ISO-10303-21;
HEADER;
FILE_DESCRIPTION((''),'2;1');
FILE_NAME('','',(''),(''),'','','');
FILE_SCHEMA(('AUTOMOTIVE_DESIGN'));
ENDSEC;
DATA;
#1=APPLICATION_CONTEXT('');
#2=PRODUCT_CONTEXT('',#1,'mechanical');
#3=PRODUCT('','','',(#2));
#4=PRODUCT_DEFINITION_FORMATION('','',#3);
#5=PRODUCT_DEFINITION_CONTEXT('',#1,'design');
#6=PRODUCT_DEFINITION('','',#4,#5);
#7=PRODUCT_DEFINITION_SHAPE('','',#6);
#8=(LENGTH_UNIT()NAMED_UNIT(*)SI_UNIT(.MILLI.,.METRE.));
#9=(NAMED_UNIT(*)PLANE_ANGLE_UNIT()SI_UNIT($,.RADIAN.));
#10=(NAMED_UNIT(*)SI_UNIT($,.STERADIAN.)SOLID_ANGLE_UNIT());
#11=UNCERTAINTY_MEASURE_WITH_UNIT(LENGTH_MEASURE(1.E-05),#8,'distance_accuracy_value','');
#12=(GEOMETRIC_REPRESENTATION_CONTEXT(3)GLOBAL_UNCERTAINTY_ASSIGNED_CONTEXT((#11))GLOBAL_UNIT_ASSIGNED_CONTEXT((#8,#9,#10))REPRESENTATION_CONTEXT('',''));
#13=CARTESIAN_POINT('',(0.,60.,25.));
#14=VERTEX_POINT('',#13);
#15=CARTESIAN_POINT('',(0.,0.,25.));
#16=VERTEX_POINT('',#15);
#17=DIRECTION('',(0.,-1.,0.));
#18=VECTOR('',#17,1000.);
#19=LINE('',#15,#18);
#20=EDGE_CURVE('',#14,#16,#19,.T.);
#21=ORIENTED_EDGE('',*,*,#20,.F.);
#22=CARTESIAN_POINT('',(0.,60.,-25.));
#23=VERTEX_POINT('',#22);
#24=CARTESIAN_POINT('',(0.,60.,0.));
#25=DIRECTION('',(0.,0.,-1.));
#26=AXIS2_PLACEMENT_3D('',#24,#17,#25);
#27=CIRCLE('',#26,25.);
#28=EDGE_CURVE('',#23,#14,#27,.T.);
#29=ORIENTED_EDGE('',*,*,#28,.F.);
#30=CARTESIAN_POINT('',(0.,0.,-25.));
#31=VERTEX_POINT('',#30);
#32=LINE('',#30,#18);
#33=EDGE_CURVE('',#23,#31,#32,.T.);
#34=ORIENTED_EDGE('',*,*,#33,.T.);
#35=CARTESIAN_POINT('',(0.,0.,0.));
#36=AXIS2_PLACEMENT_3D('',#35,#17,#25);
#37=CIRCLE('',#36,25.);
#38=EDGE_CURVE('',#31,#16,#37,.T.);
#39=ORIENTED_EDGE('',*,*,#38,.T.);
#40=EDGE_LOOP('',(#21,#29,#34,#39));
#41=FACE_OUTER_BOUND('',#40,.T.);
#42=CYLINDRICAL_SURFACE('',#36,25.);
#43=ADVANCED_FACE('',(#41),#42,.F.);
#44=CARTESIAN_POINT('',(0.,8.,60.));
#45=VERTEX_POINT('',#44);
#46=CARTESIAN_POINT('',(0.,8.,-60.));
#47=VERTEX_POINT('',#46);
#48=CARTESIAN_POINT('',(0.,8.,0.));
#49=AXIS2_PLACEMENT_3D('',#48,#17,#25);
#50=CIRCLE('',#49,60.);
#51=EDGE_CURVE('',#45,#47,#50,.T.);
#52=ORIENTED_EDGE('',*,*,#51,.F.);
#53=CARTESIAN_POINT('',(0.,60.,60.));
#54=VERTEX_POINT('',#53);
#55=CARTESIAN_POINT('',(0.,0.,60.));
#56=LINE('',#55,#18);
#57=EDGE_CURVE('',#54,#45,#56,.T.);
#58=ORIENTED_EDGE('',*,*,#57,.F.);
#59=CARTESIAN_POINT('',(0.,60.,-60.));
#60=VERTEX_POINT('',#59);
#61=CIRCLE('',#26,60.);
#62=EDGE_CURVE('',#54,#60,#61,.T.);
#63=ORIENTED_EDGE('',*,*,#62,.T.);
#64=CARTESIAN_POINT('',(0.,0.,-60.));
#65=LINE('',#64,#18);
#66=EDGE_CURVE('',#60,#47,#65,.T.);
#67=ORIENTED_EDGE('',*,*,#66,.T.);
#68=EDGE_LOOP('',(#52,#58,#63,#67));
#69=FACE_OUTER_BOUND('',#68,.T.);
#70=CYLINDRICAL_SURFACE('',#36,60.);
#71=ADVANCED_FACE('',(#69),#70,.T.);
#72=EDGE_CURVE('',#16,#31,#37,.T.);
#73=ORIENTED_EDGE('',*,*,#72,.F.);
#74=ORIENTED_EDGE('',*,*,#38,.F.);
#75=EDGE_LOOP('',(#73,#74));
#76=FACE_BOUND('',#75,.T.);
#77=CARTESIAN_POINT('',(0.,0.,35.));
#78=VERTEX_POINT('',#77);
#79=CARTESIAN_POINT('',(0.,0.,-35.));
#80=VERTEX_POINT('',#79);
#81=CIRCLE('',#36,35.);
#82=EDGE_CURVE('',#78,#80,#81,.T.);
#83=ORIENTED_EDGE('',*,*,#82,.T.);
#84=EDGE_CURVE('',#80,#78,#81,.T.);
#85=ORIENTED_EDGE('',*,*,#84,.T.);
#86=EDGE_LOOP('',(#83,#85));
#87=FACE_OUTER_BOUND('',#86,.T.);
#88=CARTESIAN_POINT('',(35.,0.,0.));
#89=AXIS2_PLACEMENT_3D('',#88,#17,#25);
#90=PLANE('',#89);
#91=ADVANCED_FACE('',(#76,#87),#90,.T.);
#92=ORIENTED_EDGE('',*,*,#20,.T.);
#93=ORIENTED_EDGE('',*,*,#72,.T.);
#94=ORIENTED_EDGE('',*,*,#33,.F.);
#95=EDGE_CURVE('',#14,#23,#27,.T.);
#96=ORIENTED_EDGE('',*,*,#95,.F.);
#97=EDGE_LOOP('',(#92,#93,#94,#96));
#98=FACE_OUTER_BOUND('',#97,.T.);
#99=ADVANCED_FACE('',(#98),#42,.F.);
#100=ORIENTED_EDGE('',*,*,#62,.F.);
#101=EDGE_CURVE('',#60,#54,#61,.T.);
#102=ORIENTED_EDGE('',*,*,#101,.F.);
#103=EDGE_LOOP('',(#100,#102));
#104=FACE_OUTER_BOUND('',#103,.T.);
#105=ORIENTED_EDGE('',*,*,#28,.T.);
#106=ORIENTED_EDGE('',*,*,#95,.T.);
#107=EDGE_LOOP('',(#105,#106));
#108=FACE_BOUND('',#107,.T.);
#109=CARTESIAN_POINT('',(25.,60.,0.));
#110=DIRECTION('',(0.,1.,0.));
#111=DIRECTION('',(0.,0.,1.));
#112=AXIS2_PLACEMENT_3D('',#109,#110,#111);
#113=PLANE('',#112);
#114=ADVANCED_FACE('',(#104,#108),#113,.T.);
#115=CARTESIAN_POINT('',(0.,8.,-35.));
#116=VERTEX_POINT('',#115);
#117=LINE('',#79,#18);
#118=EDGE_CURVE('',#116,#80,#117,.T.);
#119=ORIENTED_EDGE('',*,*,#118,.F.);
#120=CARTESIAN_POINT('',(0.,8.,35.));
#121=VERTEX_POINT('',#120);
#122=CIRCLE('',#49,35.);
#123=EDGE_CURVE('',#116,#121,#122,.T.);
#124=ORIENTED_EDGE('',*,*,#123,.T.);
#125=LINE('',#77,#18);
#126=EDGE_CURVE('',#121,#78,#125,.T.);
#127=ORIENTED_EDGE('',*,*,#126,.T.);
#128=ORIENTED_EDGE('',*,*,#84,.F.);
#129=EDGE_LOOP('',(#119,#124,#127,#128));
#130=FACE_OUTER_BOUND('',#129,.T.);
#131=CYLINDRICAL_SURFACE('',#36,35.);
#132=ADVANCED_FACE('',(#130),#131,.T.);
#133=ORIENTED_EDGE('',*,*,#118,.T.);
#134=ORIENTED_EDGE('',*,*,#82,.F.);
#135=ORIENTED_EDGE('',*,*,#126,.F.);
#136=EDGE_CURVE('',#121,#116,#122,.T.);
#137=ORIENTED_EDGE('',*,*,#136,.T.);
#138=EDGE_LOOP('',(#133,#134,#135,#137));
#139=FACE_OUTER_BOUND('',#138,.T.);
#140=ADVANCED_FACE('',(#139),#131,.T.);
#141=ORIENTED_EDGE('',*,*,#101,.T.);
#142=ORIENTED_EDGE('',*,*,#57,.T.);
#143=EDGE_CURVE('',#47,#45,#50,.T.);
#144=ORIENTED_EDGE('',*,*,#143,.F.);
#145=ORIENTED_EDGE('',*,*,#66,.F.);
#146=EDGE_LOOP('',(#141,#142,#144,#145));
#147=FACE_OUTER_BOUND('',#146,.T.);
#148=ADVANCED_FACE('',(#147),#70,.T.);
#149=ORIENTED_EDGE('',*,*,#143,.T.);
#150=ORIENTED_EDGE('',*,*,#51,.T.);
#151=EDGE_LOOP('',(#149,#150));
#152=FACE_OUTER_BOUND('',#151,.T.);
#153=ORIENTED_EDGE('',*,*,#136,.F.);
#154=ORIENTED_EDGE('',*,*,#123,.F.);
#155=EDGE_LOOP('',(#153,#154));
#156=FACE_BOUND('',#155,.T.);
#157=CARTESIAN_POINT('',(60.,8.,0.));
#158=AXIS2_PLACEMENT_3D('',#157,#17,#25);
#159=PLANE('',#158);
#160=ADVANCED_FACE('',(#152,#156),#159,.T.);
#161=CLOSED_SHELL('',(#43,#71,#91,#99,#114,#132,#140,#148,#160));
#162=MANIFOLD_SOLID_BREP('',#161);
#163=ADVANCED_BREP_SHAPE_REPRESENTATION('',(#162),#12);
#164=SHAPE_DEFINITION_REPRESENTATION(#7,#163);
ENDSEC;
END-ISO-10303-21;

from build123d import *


with BuildPart() as part:
    # Sketch1 → Revolve1 (revolve)
    with BuildSketch(Plane.XY, mode=Mode.PRIVATE) as revolve1_sk:
        Polygon((25, 0), (25, 60), (60, 60), (60, 8), (35, 8), (35, 0), align=None)
    revolve(revolve1_sk.sketch.rotate(Axis((0, 0, 0), (0, 1, 0)), 90), axis=Axis((0, 0, 0), (0, 1, 0)))


solid = part.part
